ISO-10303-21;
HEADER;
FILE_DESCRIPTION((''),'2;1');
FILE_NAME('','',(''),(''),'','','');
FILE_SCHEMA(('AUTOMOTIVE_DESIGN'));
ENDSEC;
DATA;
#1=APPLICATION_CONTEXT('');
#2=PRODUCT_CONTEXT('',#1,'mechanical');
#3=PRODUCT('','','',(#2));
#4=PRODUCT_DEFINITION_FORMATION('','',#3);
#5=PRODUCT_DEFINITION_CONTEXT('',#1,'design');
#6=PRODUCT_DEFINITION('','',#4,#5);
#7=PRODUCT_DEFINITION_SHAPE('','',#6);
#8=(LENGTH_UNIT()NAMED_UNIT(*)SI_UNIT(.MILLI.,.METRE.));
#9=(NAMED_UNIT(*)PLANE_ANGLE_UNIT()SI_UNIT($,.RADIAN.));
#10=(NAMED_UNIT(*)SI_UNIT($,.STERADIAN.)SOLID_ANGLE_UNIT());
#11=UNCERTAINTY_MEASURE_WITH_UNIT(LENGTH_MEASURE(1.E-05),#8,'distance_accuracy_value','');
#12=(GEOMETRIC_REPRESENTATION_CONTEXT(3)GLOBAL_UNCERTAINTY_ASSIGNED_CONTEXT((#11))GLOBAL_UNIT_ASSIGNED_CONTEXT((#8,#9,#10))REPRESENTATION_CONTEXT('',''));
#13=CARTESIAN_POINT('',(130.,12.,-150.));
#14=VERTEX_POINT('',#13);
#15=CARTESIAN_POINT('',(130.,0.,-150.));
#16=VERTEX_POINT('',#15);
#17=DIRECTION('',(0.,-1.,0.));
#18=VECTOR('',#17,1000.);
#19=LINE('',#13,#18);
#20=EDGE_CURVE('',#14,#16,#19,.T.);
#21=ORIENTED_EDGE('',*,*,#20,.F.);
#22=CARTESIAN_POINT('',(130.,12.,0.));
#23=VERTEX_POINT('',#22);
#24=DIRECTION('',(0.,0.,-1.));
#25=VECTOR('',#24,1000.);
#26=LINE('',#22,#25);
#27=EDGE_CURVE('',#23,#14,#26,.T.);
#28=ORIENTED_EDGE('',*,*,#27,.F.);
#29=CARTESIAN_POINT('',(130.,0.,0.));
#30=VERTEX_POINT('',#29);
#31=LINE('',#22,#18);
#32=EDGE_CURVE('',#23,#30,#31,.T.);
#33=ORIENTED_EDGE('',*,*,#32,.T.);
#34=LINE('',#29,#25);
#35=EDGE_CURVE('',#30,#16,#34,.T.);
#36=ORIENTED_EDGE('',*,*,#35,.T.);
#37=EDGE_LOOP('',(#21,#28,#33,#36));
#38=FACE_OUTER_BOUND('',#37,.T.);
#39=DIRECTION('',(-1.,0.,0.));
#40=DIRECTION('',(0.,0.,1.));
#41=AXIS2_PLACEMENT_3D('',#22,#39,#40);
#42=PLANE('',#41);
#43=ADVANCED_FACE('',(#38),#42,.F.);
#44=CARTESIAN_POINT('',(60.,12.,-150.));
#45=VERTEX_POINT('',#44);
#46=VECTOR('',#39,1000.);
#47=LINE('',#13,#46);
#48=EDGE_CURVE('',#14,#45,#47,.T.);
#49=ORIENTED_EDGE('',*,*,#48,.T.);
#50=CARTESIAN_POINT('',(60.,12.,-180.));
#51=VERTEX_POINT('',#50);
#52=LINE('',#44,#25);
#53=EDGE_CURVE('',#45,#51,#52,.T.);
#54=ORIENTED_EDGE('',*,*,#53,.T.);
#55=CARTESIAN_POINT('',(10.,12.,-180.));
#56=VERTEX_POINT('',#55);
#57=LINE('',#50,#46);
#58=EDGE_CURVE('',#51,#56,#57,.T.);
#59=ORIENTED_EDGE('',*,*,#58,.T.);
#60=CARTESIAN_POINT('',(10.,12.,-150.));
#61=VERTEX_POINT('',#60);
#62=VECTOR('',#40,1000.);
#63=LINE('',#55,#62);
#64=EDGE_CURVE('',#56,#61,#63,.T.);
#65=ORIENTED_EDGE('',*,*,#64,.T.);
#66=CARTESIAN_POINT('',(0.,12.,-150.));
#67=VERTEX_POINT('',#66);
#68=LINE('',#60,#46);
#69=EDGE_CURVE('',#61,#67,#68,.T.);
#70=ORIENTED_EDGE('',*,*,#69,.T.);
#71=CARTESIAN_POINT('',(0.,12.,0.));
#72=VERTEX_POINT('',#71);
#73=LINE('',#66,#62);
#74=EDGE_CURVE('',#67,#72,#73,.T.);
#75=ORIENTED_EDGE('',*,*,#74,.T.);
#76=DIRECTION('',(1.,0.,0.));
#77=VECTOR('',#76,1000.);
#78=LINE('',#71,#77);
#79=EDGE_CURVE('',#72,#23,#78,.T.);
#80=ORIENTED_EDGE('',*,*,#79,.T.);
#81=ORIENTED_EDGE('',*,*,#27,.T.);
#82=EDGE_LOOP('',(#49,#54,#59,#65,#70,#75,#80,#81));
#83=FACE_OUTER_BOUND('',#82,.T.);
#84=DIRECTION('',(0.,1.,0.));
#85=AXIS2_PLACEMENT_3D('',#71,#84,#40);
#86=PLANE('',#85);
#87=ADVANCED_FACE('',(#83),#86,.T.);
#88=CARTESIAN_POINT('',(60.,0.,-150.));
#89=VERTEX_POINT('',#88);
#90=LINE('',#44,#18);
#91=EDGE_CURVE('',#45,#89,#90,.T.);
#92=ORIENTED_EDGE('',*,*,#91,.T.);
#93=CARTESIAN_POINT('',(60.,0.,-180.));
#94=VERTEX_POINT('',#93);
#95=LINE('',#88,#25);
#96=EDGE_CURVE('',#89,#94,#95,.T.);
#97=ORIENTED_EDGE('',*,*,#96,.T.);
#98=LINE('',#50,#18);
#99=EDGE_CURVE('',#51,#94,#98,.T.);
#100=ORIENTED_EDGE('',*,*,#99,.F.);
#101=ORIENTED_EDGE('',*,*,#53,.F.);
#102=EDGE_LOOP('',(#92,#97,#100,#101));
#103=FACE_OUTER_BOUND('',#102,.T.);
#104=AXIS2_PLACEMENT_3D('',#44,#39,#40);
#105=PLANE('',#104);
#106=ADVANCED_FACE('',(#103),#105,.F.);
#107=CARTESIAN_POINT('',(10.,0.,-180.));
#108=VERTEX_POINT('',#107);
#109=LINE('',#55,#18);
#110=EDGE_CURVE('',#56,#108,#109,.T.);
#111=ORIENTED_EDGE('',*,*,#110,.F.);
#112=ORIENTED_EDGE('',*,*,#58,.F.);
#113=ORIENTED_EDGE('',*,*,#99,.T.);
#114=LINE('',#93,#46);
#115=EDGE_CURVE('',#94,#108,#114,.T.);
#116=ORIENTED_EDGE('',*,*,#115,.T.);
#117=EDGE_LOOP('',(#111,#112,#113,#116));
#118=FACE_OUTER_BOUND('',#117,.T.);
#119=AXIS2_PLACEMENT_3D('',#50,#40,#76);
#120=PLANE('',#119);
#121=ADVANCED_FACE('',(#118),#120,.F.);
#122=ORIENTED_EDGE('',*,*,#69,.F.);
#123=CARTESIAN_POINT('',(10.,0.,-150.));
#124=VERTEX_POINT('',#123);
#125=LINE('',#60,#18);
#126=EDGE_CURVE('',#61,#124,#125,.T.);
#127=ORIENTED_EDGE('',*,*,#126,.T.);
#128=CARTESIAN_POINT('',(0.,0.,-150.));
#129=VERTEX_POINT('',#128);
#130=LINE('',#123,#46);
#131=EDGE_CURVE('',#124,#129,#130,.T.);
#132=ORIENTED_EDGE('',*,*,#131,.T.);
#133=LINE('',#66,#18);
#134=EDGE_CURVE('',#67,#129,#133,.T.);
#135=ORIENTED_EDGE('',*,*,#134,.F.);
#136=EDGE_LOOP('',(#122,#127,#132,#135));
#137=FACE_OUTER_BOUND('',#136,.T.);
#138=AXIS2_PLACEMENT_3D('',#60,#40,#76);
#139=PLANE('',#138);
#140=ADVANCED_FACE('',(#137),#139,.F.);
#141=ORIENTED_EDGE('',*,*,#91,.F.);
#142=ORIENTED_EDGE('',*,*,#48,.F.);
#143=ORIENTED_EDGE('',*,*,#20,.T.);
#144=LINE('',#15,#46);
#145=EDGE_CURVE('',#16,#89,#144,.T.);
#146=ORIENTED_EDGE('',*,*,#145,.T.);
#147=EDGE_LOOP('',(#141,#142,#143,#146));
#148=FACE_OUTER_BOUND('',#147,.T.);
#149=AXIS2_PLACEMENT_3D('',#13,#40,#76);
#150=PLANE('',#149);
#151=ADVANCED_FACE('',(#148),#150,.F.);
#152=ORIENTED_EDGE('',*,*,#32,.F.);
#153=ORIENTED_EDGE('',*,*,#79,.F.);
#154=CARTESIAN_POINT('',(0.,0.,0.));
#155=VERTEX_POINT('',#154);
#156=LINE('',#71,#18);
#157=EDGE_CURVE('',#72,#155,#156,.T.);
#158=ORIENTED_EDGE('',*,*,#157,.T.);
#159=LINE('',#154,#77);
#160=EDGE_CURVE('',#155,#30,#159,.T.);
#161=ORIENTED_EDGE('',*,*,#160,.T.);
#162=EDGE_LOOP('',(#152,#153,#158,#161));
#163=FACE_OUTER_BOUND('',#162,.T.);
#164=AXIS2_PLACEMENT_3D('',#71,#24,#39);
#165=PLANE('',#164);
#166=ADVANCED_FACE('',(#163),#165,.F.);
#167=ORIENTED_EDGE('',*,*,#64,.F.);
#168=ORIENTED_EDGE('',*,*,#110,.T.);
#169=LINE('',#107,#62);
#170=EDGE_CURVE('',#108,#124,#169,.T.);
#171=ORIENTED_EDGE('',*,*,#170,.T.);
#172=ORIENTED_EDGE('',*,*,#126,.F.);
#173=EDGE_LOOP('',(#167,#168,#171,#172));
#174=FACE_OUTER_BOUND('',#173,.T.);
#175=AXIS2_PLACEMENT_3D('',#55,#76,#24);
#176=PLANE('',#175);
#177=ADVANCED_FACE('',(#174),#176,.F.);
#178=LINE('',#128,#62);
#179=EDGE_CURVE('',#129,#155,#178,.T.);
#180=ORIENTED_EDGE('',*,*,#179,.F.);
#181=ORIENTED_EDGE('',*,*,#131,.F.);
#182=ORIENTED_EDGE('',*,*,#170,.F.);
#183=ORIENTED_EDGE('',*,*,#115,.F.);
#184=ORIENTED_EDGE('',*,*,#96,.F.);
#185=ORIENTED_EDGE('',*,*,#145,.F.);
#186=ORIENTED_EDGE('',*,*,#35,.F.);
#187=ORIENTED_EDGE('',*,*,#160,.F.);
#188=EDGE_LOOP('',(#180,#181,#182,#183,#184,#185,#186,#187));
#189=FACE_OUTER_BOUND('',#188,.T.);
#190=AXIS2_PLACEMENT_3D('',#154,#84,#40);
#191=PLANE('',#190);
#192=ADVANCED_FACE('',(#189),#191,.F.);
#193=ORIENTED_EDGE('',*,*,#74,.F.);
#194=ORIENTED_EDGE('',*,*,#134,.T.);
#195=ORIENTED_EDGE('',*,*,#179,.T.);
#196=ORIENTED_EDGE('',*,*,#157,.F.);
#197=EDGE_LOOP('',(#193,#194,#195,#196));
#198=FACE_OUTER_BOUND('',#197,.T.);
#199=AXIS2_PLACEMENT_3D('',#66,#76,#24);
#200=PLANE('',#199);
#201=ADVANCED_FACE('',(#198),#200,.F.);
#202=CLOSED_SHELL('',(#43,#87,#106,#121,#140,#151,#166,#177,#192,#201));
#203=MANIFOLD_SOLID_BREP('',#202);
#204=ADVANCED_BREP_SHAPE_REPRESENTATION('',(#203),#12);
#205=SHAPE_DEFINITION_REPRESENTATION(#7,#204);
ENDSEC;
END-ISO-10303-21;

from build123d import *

# Parameters (mm, degrees)
EXTRUDE_1_DEPTH = 12


with BuildPart() as part:
    # 草图1 → 凸台-拉伸1 (new body)
    with BuildSketch(Plane(origin=(0, 0, 0), x_dir=(1, 0, 0), z_dir=(0, 1, 0))):
        Polygon((0, 0), (130, 0), (130, 150), (60, 150), (60, 180), (10, 180), (10, 150), (0, 150), align=None)
    extrude(amount=EXTRUDE_1_DEPTH)


solid = part.part
